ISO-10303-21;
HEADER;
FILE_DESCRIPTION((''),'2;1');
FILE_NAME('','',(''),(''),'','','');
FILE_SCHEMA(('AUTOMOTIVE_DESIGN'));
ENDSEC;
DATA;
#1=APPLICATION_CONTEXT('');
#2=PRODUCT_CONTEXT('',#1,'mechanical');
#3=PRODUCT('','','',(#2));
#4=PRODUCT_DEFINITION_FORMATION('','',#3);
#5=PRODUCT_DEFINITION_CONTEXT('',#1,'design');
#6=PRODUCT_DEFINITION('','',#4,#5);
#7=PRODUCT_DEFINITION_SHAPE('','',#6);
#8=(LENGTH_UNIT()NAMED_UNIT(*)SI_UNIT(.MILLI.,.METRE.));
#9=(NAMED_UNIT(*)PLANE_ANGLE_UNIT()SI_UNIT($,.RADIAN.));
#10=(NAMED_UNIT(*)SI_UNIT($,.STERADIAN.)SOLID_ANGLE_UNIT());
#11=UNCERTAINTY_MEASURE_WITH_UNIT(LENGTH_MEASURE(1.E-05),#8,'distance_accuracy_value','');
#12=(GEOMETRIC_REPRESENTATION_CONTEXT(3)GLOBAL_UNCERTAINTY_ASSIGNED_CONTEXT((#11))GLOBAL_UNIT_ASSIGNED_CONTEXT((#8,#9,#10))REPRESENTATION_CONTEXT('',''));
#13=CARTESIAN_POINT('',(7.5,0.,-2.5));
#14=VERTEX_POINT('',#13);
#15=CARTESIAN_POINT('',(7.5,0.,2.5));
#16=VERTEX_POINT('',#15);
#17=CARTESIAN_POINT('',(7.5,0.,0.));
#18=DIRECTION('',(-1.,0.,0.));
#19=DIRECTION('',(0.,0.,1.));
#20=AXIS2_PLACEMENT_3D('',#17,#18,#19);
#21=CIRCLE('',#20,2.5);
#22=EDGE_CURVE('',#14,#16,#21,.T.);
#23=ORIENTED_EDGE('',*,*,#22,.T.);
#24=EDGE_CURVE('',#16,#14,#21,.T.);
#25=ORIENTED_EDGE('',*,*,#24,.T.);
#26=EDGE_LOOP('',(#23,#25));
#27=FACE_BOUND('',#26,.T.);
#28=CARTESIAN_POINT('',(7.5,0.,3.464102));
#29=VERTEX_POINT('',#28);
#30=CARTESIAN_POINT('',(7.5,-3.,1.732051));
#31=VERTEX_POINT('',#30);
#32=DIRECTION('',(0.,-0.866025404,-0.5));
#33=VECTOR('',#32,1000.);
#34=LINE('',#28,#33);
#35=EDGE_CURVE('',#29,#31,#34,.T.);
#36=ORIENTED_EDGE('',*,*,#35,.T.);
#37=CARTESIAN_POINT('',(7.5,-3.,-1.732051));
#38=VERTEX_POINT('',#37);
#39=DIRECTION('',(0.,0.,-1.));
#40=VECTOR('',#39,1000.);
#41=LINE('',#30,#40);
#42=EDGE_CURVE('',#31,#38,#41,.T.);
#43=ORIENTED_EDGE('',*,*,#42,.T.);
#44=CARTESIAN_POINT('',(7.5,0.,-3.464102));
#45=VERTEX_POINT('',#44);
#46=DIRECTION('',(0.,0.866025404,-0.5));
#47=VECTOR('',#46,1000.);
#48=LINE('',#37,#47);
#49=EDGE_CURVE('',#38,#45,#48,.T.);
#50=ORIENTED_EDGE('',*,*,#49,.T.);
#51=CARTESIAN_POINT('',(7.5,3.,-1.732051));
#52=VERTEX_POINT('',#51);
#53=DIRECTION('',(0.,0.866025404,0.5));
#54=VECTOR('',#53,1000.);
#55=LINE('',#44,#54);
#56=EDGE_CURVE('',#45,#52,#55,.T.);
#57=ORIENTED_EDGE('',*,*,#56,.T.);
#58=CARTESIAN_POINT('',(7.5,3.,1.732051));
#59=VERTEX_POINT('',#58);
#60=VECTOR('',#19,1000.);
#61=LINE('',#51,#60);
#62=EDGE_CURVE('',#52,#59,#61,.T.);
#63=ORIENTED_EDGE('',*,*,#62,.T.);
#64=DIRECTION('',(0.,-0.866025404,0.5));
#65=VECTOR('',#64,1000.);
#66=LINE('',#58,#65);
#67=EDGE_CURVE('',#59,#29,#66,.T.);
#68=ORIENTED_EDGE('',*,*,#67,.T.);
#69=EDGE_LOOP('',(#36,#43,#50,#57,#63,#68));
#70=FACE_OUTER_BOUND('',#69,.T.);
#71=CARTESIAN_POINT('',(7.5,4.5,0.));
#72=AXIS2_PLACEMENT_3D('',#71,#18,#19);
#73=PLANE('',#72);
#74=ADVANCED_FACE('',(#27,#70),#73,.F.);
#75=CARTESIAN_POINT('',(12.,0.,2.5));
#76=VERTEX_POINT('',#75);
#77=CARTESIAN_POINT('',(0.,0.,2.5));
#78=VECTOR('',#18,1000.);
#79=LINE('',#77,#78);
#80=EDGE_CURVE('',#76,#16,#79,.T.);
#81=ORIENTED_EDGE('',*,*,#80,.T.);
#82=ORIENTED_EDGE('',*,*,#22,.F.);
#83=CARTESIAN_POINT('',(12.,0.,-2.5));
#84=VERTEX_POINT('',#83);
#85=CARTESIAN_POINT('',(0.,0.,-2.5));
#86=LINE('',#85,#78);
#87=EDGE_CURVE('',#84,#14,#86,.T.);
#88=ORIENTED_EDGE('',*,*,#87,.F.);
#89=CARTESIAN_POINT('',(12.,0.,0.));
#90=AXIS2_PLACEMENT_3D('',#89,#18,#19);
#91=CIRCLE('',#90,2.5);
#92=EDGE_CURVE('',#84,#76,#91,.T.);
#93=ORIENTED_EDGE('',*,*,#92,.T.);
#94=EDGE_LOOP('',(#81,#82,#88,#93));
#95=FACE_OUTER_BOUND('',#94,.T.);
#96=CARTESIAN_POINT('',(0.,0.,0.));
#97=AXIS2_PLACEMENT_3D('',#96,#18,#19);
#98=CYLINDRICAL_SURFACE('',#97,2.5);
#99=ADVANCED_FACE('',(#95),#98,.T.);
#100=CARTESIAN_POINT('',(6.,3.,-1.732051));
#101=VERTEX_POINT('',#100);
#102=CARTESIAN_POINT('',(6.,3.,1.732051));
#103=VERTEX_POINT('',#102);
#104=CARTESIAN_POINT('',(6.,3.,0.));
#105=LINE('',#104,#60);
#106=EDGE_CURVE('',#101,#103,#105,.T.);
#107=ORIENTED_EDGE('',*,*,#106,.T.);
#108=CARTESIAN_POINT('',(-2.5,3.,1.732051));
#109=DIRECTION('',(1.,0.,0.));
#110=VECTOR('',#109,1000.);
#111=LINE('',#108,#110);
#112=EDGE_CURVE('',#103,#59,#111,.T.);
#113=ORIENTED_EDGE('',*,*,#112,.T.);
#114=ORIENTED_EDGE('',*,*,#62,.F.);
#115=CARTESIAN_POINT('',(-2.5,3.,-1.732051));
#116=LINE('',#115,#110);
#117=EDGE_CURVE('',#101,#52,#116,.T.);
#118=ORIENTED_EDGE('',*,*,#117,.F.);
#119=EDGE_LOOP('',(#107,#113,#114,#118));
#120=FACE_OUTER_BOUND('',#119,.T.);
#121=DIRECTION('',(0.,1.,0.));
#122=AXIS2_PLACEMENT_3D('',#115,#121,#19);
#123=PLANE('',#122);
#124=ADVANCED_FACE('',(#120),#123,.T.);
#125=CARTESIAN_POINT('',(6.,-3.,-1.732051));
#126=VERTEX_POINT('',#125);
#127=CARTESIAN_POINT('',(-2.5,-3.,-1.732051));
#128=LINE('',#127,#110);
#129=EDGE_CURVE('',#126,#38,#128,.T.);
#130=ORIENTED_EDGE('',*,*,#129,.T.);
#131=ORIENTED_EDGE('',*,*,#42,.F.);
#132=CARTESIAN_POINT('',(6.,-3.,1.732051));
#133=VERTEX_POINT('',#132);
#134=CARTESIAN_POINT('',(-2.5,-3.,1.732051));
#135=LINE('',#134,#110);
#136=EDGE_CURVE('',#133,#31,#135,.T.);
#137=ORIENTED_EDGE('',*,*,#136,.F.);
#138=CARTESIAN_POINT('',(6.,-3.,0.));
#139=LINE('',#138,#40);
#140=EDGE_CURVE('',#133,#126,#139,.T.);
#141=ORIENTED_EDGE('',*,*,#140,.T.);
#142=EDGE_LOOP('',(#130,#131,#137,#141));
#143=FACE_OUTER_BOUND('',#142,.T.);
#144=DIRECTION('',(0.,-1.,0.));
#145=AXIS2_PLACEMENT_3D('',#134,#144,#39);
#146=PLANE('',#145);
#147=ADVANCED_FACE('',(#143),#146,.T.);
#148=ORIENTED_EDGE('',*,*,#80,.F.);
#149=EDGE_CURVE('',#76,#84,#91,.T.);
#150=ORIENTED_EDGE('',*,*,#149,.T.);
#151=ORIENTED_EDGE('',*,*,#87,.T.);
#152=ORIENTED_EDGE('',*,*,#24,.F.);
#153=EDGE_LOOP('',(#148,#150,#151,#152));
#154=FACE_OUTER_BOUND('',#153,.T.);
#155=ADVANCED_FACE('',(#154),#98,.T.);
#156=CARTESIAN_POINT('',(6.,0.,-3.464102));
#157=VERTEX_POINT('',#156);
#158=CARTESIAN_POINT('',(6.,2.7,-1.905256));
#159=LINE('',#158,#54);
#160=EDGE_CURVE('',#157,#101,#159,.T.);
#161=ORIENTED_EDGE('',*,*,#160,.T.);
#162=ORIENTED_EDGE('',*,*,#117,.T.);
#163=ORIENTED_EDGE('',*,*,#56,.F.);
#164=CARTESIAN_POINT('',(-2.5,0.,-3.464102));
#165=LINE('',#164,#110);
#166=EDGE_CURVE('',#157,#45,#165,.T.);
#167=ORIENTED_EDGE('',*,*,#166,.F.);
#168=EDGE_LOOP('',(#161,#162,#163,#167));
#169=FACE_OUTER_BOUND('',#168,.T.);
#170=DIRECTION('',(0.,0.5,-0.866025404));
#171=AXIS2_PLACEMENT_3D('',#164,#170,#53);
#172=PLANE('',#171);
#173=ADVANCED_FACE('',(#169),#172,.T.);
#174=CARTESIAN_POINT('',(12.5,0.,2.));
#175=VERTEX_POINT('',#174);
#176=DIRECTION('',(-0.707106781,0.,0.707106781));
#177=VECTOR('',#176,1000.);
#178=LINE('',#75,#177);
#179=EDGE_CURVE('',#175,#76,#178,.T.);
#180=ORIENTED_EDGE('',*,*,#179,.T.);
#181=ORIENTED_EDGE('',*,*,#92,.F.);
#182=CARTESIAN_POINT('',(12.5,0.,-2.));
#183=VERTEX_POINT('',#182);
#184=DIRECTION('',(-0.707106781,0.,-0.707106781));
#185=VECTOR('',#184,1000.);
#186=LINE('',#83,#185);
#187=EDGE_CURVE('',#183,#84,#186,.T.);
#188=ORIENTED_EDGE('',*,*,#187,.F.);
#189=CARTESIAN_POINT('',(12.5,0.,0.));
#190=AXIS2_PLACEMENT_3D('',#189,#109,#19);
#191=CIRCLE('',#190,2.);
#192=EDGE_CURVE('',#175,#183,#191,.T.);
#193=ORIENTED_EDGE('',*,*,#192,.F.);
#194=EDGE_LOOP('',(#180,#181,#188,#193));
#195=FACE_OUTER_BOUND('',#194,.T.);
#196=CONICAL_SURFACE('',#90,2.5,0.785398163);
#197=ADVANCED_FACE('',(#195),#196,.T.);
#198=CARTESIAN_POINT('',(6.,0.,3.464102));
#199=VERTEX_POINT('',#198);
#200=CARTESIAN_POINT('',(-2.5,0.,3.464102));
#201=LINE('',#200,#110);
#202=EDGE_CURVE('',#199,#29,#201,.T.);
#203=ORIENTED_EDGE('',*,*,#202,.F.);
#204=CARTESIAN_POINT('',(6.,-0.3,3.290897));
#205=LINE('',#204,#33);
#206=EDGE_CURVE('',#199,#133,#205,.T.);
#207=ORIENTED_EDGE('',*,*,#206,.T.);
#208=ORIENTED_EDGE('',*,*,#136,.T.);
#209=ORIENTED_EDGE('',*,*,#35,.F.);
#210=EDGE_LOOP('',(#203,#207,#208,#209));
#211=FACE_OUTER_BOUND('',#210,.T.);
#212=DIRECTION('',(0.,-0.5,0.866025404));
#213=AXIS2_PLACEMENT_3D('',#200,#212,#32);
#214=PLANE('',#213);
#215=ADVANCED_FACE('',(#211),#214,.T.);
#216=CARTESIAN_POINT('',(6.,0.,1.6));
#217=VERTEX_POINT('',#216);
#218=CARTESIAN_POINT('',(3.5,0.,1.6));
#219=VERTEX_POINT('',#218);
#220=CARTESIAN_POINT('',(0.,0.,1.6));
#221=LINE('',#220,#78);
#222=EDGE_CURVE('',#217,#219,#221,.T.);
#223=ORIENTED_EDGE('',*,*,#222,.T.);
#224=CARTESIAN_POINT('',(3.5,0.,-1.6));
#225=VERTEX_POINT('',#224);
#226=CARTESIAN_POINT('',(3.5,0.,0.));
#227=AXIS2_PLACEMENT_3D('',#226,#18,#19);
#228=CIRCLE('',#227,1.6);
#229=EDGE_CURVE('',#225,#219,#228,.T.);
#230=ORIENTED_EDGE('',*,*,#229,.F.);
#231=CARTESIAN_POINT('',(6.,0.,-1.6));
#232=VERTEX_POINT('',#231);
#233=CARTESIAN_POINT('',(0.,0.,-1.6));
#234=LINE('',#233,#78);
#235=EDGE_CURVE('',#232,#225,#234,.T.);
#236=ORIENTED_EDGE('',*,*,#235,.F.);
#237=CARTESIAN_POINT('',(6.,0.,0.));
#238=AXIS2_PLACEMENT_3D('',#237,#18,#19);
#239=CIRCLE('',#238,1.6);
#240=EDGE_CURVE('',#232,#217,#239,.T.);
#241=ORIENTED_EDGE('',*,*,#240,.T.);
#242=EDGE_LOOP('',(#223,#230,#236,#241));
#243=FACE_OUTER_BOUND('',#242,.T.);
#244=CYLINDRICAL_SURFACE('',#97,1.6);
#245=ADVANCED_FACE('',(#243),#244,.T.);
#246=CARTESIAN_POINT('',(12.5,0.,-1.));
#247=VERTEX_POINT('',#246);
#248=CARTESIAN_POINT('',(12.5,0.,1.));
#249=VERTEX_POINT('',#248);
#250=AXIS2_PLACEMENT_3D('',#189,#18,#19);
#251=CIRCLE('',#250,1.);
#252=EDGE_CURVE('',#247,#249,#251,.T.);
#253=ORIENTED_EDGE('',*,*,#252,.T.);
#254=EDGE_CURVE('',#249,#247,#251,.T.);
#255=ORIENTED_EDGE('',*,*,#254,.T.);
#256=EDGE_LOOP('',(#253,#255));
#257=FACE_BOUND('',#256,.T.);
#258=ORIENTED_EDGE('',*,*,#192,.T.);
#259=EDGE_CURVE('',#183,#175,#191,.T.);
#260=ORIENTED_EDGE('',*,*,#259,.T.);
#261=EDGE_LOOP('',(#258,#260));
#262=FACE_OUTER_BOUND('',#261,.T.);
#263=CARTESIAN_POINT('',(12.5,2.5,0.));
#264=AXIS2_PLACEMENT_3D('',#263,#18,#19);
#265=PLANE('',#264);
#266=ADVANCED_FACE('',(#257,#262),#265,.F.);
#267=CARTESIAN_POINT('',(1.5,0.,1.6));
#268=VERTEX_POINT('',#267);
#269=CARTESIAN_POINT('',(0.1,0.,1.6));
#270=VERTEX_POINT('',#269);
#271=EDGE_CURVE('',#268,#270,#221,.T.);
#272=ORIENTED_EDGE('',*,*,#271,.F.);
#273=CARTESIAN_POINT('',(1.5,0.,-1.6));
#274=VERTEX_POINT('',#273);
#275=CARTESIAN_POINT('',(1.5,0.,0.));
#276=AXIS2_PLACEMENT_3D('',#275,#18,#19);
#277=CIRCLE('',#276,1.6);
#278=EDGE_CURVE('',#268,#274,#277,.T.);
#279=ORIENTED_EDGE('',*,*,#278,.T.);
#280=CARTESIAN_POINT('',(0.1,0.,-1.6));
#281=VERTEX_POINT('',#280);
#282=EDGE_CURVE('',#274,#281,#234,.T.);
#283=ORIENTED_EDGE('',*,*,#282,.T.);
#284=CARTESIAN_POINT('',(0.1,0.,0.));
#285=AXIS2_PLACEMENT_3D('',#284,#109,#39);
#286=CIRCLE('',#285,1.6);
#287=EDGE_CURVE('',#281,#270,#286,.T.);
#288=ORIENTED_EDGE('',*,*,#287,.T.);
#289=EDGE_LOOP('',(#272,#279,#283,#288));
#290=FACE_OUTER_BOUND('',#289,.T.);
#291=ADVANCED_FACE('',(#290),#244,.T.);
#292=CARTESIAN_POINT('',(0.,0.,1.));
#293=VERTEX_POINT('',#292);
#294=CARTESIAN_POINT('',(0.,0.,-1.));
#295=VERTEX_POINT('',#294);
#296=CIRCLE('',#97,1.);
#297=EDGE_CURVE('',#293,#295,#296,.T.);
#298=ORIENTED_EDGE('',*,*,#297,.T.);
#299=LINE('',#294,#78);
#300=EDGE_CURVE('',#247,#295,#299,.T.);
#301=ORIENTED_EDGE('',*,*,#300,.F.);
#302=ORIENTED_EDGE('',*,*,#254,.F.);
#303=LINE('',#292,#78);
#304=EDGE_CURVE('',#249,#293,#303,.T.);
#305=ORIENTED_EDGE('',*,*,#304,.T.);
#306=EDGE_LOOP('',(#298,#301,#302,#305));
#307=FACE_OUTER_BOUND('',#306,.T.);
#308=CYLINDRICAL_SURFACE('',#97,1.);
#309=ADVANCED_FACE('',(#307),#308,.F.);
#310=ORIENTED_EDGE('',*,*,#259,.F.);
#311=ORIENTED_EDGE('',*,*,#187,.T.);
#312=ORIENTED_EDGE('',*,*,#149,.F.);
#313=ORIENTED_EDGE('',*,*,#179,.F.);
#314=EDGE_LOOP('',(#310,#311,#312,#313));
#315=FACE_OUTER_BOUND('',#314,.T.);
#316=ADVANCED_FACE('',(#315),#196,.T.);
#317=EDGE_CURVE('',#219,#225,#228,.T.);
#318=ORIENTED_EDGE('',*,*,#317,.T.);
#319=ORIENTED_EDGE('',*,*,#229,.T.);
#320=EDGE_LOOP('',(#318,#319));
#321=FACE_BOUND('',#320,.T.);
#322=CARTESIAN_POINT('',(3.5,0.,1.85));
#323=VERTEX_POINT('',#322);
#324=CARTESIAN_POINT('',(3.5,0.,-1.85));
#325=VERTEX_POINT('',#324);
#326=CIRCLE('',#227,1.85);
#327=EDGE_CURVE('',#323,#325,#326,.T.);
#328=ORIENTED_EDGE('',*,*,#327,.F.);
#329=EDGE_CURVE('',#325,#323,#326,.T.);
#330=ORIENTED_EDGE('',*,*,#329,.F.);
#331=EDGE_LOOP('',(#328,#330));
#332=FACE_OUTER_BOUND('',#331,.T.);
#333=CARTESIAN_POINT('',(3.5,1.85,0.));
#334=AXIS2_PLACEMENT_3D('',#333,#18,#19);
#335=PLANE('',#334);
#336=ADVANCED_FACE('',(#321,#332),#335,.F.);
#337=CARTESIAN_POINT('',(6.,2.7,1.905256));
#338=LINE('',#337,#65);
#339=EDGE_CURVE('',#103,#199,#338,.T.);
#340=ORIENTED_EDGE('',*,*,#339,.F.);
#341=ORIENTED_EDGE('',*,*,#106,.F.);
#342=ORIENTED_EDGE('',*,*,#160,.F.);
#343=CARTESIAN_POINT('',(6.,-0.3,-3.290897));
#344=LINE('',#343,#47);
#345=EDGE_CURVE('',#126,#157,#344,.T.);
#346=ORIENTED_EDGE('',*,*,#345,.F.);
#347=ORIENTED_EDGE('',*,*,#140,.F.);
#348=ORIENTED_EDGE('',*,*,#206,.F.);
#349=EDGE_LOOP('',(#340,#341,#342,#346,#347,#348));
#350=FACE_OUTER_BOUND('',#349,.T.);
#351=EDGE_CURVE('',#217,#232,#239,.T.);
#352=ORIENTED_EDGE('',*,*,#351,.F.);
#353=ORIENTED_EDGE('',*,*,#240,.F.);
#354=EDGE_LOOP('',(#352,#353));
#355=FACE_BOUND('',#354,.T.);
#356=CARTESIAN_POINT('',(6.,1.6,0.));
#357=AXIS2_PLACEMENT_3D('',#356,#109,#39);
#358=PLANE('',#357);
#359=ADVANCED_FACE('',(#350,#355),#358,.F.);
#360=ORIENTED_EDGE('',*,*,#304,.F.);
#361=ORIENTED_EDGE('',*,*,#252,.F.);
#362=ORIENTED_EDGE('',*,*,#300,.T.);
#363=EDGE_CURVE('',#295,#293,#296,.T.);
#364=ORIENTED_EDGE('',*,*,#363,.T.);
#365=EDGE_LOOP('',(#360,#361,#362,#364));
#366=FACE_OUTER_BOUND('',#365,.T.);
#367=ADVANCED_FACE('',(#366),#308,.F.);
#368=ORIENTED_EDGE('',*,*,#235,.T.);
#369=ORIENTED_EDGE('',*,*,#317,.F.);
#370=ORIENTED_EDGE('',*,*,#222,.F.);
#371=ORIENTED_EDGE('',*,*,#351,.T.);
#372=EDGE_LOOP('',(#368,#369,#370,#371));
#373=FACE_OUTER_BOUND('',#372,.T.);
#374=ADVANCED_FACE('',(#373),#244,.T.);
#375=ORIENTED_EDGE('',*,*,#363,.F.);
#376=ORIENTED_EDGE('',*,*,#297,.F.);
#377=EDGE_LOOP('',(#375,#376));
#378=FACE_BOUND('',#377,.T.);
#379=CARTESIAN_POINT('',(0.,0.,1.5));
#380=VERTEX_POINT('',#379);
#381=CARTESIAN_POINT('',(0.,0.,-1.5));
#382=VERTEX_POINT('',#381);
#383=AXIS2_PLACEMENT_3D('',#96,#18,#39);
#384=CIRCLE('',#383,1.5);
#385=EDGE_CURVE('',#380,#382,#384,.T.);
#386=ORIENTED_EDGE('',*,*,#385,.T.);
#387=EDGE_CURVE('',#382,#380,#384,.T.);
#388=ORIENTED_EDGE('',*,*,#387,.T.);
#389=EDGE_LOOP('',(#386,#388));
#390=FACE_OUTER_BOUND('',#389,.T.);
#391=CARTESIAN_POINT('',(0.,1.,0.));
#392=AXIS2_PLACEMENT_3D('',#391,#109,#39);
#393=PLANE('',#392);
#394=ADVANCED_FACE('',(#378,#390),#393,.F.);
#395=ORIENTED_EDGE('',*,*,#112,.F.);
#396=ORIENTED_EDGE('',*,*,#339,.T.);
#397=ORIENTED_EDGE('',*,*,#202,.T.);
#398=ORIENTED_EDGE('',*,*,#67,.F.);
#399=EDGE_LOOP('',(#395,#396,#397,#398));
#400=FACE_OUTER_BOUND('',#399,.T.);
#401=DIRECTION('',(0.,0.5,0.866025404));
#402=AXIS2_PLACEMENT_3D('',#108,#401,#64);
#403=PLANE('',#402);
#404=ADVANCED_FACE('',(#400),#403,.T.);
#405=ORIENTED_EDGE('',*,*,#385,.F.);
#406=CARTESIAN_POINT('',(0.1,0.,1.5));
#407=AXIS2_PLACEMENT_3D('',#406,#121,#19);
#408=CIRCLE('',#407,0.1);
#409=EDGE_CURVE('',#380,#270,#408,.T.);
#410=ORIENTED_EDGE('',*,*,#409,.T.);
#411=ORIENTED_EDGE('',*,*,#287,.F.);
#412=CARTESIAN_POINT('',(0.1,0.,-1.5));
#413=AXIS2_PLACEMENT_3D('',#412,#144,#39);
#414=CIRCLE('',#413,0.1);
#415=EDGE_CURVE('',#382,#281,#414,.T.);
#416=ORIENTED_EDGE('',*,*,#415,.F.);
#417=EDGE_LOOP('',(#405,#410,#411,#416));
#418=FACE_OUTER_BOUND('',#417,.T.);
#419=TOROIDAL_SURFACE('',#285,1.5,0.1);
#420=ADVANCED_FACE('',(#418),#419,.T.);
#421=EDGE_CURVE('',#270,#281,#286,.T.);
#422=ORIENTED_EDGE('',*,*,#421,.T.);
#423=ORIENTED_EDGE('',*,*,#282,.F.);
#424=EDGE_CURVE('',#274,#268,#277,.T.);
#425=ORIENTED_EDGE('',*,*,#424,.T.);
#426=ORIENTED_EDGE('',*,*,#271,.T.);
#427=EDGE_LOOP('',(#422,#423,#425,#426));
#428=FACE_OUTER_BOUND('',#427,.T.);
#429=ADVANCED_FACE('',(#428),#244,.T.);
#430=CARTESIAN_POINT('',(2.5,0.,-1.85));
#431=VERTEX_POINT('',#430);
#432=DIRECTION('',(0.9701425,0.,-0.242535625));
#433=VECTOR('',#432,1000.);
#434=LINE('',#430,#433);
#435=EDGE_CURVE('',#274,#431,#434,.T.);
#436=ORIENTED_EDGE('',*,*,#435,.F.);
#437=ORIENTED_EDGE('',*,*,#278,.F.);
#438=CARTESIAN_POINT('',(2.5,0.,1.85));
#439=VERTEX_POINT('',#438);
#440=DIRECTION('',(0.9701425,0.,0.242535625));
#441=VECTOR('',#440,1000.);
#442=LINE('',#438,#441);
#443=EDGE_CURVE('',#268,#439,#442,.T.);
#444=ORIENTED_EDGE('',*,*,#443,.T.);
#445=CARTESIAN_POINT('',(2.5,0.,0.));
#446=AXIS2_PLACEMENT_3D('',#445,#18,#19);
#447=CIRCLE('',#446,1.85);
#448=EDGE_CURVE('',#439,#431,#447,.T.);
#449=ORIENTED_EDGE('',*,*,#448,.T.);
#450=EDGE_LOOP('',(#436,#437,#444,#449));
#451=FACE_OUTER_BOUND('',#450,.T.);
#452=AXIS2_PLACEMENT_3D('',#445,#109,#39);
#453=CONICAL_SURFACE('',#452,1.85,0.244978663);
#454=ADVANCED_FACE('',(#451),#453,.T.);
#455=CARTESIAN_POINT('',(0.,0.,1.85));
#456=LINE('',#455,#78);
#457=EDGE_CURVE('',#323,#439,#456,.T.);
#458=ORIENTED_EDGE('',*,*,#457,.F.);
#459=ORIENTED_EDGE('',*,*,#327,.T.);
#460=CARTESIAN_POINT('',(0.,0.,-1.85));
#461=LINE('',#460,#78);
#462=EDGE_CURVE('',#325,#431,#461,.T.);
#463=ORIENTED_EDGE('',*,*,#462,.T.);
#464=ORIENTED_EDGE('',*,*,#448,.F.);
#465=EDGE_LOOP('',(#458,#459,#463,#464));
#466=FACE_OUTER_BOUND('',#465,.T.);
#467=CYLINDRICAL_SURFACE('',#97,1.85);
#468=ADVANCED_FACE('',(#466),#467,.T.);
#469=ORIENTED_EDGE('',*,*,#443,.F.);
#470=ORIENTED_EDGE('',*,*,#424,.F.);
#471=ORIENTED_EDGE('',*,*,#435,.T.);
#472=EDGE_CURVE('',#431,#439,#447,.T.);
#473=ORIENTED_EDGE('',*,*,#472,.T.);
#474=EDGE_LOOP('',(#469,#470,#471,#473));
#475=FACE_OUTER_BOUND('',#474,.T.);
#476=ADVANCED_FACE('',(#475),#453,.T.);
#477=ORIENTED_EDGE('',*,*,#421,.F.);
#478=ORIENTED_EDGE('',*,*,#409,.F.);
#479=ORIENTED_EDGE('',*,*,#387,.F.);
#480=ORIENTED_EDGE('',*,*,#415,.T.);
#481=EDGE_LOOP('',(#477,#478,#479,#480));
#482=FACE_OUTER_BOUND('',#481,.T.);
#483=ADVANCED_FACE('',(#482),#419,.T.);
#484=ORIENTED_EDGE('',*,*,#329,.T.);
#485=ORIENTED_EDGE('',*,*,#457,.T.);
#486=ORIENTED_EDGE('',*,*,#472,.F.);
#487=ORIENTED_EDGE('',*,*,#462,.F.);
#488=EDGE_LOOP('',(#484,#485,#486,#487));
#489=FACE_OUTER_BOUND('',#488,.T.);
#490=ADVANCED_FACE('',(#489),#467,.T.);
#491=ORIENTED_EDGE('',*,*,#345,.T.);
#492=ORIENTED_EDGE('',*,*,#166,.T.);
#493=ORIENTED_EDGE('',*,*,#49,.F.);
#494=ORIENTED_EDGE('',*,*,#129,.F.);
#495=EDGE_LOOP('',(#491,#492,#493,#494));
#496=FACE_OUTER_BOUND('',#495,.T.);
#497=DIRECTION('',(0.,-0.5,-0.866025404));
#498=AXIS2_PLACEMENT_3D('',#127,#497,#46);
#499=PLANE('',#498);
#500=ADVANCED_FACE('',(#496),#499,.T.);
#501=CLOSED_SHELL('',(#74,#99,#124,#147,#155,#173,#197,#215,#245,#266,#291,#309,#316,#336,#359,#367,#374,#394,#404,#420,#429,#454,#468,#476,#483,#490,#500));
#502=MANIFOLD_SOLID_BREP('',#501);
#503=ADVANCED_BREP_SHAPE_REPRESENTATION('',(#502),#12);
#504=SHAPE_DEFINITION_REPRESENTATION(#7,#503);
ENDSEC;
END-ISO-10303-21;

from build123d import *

# Parameters (mm, degrees)
SKETCH2_OUTSIDE_W  = 14.568
SKETCH2_OUTSIDE_H  = 14.568
CUT_EXTRUDE3_DEPTH = 10
FILLET1_R          = 0.1
CHAMFER1_SIZE      = 0.5


with BuildPart() as part:
    # Sketch1 → Revolve1 (revolve)
    with BuildSketch(Plane.XY, mode=Mode.PRIVATE) as revolve1_sk:
        Polygon((0, 1), (12.5, 1), (12.5, 2.5), (7.5, 2.5), (7.5, 4.5), (6, 4.5), (6, 1.6), (3.5, 1.6), (3.5, 1.85), (2.5, 1.85), (1.5, 1.6), (0, 1.6), align=None)
    revolve(revolve1_sk.sketch.rotate(Axis((0, 0, 0), (1, 0, 0)), 90), axis=Axis((0, 0, 0), (1, 0, 0)))

    # Sketch2 outside → Cut-Extrude3 (cut)
    with BuildSketch(Plane(origin=(7.5, 0, 0), x_dir=(0, 0, -1), z_dir=(1, 0, 0))):
        Rectangle(SKETCH2_OUTSIDE_W, SKETCH2_OUTSIDE_H)
        Polygon((1.732050808, -3), (3.464101615, 0), (1.732050808, 3), (-1.732050808, 3), (-3.464101615, 0), (-1.732050808, -3), align=None, mode=Mode.SUBTRACT)
    extrude(amount=-CUT_EXTRUDE3_DEPTH, mode=Mode.SUBTRACT)

    # Fillet1
    fillet1_edges = [part.edges().sort_by_distance(p)[0] for p in [
        (0, 0, -1.6),
    ]]
    fillet(fillet1_edges, radius=FILLET1_R)

    # Chamfer1
    chamfer1_edges = [part.edges().sort_by_distance(p)[0] for p in [
        (12.5, 0, -2.5),
    ]]
    chamfer(chamfer1_edges, length=CHAMFER1_SIZE)


solid = part.part
